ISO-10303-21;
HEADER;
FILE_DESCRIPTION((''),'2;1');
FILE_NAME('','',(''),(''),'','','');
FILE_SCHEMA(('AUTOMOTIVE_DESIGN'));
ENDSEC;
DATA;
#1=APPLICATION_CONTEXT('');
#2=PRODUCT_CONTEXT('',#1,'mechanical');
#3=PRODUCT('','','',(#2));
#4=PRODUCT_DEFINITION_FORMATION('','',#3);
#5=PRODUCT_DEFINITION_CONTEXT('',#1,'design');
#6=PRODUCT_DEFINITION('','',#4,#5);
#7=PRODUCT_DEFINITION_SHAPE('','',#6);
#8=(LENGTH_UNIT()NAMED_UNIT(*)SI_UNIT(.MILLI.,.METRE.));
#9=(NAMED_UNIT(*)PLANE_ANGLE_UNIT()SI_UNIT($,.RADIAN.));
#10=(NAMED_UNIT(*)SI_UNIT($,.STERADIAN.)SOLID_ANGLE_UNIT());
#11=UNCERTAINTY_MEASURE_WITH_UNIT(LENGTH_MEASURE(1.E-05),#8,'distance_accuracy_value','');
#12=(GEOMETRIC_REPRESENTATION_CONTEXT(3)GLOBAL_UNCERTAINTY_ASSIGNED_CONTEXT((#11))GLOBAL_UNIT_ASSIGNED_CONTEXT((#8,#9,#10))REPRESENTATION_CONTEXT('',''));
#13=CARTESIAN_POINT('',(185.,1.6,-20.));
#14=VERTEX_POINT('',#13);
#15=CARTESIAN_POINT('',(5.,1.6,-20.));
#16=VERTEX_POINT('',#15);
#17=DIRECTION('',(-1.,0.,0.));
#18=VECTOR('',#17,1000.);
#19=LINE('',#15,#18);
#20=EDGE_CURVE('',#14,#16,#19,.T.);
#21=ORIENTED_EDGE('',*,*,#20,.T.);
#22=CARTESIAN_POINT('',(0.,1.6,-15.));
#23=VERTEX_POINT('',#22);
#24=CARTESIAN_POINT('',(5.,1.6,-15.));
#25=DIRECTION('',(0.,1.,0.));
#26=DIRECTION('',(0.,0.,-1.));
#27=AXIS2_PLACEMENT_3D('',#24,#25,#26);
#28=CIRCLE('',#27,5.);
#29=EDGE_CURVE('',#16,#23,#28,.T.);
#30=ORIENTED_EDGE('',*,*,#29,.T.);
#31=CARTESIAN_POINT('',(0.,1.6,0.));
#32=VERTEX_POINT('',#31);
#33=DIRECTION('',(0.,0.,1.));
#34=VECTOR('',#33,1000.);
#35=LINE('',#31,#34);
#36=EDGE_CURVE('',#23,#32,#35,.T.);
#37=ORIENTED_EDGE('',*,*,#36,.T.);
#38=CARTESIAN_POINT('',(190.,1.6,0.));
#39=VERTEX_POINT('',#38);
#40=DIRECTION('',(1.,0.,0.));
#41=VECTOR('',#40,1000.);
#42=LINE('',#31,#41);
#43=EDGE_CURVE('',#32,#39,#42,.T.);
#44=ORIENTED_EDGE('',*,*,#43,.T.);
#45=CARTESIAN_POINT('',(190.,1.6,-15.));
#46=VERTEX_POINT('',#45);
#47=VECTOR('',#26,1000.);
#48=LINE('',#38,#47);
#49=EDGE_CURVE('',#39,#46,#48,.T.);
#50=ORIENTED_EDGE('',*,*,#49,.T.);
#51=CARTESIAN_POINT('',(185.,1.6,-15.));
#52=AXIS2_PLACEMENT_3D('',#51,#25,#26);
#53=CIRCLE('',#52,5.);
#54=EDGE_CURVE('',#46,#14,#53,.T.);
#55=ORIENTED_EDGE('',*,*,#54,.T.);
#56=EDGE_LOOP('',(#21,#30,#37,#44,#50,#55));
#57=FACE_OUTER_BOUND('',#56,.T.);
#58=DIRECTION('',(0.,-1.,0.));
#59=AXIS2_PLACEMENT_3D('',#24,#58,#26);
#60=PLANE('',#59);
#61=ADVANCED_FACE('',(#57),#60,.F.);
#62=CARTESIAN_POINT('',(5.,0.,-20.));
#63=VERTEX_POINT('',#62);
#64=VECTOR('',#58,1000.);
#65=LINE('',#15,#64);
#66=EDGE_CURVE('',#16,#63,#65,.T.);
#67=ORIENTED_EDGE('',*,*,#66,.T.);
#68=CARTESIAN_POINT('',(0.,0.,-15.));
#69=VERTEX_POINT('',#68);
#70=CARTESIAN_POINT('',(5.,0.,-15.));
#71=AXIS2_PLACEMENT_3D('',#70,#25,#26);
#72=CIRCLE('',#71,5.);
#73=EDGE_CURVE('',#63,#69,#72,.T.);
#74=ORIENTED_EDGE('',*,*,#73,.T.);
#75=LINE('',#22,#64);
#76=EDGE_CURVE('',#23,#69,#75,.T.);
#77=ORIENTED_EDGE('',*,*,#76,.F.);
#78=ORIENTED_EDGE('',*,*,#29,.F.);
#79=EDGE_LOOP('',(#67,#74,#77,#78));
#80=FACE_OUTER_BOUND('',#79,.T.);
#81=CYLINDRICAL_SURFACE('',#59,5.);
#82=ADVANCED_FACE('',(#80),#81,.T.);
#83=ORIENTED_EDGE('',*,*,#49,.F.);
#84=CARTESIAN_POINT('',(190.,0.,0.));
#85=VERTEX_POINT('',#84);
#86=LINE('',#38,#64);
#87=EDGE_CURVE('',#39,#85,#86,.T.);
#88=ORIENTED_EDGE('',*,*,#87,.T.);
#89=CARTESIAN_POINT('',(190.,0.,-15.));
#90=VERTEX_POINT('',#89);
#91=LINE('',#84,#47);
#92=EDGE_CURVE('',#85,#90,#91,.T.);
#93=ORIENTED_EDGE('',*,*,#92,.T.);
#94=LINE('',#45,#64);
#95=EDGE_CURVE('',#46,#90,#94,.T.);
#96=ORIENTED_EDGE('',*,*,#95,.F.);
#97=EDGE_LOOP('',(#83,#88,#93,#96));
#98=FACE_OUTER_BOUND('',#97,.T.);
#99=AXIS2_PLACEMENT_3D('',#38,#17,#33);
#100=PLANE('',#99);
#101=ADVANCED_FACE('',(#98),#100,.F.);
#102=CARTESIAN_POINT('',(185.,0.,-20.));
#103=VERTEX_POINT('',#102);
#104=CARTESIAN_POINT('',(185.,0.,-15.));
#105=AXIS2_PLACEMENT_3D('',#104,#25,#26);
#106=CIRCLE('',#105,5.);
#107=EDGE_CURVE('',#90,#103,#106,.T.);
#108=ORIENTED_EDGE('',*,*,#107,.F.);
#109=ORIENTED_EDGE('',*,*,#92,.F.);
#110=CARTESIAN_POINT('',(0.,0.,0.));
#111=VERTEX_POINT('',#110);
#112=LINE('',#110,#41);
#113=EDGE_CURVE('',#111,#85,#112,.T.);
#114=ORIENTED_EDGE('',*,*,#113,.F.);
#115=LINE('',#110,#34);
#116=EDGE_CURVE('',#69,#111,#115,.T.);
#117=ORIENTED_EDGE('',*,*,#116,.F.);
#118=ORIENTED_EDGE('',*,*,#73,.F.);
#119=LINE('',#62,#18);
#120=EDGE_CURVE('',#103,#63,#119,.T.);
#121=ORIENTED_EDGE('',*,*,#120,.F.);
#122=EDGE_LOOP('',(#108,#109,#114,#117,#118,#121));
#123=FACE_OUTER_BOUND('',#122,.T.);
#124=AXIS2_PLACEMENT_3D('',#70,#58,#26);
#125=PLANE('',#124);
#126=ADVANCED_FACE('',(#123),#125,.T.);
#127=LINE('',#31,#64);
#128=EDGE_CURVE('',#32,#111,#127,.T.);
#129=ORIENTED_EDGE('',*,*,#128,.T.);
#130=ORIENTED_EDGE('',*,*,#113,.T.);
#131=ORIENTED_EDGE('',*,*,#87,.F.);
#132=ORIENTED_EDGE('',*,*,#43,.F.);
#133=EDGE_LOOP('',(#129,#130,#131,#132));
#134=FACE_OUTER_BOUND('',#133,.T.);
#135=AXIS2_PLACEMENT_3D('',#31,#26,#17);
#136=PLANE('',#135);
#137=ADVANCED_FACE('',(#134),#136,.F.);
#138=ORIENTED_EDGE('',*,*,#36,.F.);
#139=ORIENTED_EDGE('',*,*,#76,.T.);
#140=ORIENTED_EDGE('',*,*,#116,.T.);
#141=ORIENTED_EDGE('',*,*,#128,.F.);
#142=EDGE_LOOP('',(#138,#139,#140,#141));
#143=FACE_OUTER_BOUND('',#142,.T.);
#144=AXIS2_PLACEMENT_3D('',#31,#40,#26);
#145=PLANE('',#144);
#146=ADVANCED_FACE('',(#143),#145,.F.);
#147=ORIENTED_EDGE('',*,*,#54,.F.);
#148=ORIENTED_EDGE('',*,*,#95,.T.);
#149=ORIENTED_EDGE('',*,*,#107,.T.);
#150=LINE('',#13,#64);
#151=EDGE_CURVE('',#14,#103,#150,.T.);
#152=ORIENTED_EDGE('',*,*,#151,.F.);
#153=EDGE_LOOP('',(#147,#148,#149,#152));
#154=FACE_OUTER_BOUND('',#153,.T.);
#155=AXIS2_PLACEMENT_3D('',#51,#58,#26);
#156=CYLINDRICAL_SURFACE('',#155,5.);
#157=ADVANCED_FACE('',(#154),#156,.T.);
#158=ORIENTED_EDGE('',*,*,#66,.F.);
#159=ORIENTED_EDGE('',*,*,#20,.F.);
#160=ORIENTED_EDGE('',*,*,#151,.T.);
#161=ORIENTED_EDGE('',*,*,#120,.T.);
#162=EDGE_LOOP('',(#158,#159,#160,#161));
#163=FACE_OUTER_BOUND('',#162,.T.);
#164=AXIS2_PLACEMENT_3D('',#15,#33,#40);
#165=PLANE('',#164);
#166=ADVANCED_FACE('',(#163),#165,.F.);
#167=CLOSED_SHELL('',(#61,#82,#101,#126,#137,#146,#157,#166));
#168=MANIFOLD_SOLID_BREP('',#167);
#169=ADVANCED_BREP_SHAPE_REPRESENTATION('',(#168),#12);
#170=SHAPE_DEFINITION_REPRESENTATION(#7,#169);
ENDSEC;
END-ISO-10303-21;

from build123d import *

# Parameters (mm, degrees)
BOSS_EXTRUDE1_DEPTH = 1.6


with BuildPart() as part:
    # Sketch1 → Boss-Extrude1 (new body)
    with BuildSketch(Plane(origin=(0, 0, 0), x_dir=(1, 0, 0), z_dir=(0, 1, 0))):
        with BuildLine():
            Line((0, 0), (190, 0))
            Line((190, 0), (190, 15))
            ThreePointArc((190, 15), (188.535533906, 18.535533906), (185, 20))
            Line((185, 20), (5, 20))
            ThreePointArc((5, 20), (1.464466094, 18.535533906), (0, 15))
            Line((0, 15), (0, 0))
        make_face()
    extrude(amount=BOSS_EXTRUDE1_DEPTH)


solid = part.part
